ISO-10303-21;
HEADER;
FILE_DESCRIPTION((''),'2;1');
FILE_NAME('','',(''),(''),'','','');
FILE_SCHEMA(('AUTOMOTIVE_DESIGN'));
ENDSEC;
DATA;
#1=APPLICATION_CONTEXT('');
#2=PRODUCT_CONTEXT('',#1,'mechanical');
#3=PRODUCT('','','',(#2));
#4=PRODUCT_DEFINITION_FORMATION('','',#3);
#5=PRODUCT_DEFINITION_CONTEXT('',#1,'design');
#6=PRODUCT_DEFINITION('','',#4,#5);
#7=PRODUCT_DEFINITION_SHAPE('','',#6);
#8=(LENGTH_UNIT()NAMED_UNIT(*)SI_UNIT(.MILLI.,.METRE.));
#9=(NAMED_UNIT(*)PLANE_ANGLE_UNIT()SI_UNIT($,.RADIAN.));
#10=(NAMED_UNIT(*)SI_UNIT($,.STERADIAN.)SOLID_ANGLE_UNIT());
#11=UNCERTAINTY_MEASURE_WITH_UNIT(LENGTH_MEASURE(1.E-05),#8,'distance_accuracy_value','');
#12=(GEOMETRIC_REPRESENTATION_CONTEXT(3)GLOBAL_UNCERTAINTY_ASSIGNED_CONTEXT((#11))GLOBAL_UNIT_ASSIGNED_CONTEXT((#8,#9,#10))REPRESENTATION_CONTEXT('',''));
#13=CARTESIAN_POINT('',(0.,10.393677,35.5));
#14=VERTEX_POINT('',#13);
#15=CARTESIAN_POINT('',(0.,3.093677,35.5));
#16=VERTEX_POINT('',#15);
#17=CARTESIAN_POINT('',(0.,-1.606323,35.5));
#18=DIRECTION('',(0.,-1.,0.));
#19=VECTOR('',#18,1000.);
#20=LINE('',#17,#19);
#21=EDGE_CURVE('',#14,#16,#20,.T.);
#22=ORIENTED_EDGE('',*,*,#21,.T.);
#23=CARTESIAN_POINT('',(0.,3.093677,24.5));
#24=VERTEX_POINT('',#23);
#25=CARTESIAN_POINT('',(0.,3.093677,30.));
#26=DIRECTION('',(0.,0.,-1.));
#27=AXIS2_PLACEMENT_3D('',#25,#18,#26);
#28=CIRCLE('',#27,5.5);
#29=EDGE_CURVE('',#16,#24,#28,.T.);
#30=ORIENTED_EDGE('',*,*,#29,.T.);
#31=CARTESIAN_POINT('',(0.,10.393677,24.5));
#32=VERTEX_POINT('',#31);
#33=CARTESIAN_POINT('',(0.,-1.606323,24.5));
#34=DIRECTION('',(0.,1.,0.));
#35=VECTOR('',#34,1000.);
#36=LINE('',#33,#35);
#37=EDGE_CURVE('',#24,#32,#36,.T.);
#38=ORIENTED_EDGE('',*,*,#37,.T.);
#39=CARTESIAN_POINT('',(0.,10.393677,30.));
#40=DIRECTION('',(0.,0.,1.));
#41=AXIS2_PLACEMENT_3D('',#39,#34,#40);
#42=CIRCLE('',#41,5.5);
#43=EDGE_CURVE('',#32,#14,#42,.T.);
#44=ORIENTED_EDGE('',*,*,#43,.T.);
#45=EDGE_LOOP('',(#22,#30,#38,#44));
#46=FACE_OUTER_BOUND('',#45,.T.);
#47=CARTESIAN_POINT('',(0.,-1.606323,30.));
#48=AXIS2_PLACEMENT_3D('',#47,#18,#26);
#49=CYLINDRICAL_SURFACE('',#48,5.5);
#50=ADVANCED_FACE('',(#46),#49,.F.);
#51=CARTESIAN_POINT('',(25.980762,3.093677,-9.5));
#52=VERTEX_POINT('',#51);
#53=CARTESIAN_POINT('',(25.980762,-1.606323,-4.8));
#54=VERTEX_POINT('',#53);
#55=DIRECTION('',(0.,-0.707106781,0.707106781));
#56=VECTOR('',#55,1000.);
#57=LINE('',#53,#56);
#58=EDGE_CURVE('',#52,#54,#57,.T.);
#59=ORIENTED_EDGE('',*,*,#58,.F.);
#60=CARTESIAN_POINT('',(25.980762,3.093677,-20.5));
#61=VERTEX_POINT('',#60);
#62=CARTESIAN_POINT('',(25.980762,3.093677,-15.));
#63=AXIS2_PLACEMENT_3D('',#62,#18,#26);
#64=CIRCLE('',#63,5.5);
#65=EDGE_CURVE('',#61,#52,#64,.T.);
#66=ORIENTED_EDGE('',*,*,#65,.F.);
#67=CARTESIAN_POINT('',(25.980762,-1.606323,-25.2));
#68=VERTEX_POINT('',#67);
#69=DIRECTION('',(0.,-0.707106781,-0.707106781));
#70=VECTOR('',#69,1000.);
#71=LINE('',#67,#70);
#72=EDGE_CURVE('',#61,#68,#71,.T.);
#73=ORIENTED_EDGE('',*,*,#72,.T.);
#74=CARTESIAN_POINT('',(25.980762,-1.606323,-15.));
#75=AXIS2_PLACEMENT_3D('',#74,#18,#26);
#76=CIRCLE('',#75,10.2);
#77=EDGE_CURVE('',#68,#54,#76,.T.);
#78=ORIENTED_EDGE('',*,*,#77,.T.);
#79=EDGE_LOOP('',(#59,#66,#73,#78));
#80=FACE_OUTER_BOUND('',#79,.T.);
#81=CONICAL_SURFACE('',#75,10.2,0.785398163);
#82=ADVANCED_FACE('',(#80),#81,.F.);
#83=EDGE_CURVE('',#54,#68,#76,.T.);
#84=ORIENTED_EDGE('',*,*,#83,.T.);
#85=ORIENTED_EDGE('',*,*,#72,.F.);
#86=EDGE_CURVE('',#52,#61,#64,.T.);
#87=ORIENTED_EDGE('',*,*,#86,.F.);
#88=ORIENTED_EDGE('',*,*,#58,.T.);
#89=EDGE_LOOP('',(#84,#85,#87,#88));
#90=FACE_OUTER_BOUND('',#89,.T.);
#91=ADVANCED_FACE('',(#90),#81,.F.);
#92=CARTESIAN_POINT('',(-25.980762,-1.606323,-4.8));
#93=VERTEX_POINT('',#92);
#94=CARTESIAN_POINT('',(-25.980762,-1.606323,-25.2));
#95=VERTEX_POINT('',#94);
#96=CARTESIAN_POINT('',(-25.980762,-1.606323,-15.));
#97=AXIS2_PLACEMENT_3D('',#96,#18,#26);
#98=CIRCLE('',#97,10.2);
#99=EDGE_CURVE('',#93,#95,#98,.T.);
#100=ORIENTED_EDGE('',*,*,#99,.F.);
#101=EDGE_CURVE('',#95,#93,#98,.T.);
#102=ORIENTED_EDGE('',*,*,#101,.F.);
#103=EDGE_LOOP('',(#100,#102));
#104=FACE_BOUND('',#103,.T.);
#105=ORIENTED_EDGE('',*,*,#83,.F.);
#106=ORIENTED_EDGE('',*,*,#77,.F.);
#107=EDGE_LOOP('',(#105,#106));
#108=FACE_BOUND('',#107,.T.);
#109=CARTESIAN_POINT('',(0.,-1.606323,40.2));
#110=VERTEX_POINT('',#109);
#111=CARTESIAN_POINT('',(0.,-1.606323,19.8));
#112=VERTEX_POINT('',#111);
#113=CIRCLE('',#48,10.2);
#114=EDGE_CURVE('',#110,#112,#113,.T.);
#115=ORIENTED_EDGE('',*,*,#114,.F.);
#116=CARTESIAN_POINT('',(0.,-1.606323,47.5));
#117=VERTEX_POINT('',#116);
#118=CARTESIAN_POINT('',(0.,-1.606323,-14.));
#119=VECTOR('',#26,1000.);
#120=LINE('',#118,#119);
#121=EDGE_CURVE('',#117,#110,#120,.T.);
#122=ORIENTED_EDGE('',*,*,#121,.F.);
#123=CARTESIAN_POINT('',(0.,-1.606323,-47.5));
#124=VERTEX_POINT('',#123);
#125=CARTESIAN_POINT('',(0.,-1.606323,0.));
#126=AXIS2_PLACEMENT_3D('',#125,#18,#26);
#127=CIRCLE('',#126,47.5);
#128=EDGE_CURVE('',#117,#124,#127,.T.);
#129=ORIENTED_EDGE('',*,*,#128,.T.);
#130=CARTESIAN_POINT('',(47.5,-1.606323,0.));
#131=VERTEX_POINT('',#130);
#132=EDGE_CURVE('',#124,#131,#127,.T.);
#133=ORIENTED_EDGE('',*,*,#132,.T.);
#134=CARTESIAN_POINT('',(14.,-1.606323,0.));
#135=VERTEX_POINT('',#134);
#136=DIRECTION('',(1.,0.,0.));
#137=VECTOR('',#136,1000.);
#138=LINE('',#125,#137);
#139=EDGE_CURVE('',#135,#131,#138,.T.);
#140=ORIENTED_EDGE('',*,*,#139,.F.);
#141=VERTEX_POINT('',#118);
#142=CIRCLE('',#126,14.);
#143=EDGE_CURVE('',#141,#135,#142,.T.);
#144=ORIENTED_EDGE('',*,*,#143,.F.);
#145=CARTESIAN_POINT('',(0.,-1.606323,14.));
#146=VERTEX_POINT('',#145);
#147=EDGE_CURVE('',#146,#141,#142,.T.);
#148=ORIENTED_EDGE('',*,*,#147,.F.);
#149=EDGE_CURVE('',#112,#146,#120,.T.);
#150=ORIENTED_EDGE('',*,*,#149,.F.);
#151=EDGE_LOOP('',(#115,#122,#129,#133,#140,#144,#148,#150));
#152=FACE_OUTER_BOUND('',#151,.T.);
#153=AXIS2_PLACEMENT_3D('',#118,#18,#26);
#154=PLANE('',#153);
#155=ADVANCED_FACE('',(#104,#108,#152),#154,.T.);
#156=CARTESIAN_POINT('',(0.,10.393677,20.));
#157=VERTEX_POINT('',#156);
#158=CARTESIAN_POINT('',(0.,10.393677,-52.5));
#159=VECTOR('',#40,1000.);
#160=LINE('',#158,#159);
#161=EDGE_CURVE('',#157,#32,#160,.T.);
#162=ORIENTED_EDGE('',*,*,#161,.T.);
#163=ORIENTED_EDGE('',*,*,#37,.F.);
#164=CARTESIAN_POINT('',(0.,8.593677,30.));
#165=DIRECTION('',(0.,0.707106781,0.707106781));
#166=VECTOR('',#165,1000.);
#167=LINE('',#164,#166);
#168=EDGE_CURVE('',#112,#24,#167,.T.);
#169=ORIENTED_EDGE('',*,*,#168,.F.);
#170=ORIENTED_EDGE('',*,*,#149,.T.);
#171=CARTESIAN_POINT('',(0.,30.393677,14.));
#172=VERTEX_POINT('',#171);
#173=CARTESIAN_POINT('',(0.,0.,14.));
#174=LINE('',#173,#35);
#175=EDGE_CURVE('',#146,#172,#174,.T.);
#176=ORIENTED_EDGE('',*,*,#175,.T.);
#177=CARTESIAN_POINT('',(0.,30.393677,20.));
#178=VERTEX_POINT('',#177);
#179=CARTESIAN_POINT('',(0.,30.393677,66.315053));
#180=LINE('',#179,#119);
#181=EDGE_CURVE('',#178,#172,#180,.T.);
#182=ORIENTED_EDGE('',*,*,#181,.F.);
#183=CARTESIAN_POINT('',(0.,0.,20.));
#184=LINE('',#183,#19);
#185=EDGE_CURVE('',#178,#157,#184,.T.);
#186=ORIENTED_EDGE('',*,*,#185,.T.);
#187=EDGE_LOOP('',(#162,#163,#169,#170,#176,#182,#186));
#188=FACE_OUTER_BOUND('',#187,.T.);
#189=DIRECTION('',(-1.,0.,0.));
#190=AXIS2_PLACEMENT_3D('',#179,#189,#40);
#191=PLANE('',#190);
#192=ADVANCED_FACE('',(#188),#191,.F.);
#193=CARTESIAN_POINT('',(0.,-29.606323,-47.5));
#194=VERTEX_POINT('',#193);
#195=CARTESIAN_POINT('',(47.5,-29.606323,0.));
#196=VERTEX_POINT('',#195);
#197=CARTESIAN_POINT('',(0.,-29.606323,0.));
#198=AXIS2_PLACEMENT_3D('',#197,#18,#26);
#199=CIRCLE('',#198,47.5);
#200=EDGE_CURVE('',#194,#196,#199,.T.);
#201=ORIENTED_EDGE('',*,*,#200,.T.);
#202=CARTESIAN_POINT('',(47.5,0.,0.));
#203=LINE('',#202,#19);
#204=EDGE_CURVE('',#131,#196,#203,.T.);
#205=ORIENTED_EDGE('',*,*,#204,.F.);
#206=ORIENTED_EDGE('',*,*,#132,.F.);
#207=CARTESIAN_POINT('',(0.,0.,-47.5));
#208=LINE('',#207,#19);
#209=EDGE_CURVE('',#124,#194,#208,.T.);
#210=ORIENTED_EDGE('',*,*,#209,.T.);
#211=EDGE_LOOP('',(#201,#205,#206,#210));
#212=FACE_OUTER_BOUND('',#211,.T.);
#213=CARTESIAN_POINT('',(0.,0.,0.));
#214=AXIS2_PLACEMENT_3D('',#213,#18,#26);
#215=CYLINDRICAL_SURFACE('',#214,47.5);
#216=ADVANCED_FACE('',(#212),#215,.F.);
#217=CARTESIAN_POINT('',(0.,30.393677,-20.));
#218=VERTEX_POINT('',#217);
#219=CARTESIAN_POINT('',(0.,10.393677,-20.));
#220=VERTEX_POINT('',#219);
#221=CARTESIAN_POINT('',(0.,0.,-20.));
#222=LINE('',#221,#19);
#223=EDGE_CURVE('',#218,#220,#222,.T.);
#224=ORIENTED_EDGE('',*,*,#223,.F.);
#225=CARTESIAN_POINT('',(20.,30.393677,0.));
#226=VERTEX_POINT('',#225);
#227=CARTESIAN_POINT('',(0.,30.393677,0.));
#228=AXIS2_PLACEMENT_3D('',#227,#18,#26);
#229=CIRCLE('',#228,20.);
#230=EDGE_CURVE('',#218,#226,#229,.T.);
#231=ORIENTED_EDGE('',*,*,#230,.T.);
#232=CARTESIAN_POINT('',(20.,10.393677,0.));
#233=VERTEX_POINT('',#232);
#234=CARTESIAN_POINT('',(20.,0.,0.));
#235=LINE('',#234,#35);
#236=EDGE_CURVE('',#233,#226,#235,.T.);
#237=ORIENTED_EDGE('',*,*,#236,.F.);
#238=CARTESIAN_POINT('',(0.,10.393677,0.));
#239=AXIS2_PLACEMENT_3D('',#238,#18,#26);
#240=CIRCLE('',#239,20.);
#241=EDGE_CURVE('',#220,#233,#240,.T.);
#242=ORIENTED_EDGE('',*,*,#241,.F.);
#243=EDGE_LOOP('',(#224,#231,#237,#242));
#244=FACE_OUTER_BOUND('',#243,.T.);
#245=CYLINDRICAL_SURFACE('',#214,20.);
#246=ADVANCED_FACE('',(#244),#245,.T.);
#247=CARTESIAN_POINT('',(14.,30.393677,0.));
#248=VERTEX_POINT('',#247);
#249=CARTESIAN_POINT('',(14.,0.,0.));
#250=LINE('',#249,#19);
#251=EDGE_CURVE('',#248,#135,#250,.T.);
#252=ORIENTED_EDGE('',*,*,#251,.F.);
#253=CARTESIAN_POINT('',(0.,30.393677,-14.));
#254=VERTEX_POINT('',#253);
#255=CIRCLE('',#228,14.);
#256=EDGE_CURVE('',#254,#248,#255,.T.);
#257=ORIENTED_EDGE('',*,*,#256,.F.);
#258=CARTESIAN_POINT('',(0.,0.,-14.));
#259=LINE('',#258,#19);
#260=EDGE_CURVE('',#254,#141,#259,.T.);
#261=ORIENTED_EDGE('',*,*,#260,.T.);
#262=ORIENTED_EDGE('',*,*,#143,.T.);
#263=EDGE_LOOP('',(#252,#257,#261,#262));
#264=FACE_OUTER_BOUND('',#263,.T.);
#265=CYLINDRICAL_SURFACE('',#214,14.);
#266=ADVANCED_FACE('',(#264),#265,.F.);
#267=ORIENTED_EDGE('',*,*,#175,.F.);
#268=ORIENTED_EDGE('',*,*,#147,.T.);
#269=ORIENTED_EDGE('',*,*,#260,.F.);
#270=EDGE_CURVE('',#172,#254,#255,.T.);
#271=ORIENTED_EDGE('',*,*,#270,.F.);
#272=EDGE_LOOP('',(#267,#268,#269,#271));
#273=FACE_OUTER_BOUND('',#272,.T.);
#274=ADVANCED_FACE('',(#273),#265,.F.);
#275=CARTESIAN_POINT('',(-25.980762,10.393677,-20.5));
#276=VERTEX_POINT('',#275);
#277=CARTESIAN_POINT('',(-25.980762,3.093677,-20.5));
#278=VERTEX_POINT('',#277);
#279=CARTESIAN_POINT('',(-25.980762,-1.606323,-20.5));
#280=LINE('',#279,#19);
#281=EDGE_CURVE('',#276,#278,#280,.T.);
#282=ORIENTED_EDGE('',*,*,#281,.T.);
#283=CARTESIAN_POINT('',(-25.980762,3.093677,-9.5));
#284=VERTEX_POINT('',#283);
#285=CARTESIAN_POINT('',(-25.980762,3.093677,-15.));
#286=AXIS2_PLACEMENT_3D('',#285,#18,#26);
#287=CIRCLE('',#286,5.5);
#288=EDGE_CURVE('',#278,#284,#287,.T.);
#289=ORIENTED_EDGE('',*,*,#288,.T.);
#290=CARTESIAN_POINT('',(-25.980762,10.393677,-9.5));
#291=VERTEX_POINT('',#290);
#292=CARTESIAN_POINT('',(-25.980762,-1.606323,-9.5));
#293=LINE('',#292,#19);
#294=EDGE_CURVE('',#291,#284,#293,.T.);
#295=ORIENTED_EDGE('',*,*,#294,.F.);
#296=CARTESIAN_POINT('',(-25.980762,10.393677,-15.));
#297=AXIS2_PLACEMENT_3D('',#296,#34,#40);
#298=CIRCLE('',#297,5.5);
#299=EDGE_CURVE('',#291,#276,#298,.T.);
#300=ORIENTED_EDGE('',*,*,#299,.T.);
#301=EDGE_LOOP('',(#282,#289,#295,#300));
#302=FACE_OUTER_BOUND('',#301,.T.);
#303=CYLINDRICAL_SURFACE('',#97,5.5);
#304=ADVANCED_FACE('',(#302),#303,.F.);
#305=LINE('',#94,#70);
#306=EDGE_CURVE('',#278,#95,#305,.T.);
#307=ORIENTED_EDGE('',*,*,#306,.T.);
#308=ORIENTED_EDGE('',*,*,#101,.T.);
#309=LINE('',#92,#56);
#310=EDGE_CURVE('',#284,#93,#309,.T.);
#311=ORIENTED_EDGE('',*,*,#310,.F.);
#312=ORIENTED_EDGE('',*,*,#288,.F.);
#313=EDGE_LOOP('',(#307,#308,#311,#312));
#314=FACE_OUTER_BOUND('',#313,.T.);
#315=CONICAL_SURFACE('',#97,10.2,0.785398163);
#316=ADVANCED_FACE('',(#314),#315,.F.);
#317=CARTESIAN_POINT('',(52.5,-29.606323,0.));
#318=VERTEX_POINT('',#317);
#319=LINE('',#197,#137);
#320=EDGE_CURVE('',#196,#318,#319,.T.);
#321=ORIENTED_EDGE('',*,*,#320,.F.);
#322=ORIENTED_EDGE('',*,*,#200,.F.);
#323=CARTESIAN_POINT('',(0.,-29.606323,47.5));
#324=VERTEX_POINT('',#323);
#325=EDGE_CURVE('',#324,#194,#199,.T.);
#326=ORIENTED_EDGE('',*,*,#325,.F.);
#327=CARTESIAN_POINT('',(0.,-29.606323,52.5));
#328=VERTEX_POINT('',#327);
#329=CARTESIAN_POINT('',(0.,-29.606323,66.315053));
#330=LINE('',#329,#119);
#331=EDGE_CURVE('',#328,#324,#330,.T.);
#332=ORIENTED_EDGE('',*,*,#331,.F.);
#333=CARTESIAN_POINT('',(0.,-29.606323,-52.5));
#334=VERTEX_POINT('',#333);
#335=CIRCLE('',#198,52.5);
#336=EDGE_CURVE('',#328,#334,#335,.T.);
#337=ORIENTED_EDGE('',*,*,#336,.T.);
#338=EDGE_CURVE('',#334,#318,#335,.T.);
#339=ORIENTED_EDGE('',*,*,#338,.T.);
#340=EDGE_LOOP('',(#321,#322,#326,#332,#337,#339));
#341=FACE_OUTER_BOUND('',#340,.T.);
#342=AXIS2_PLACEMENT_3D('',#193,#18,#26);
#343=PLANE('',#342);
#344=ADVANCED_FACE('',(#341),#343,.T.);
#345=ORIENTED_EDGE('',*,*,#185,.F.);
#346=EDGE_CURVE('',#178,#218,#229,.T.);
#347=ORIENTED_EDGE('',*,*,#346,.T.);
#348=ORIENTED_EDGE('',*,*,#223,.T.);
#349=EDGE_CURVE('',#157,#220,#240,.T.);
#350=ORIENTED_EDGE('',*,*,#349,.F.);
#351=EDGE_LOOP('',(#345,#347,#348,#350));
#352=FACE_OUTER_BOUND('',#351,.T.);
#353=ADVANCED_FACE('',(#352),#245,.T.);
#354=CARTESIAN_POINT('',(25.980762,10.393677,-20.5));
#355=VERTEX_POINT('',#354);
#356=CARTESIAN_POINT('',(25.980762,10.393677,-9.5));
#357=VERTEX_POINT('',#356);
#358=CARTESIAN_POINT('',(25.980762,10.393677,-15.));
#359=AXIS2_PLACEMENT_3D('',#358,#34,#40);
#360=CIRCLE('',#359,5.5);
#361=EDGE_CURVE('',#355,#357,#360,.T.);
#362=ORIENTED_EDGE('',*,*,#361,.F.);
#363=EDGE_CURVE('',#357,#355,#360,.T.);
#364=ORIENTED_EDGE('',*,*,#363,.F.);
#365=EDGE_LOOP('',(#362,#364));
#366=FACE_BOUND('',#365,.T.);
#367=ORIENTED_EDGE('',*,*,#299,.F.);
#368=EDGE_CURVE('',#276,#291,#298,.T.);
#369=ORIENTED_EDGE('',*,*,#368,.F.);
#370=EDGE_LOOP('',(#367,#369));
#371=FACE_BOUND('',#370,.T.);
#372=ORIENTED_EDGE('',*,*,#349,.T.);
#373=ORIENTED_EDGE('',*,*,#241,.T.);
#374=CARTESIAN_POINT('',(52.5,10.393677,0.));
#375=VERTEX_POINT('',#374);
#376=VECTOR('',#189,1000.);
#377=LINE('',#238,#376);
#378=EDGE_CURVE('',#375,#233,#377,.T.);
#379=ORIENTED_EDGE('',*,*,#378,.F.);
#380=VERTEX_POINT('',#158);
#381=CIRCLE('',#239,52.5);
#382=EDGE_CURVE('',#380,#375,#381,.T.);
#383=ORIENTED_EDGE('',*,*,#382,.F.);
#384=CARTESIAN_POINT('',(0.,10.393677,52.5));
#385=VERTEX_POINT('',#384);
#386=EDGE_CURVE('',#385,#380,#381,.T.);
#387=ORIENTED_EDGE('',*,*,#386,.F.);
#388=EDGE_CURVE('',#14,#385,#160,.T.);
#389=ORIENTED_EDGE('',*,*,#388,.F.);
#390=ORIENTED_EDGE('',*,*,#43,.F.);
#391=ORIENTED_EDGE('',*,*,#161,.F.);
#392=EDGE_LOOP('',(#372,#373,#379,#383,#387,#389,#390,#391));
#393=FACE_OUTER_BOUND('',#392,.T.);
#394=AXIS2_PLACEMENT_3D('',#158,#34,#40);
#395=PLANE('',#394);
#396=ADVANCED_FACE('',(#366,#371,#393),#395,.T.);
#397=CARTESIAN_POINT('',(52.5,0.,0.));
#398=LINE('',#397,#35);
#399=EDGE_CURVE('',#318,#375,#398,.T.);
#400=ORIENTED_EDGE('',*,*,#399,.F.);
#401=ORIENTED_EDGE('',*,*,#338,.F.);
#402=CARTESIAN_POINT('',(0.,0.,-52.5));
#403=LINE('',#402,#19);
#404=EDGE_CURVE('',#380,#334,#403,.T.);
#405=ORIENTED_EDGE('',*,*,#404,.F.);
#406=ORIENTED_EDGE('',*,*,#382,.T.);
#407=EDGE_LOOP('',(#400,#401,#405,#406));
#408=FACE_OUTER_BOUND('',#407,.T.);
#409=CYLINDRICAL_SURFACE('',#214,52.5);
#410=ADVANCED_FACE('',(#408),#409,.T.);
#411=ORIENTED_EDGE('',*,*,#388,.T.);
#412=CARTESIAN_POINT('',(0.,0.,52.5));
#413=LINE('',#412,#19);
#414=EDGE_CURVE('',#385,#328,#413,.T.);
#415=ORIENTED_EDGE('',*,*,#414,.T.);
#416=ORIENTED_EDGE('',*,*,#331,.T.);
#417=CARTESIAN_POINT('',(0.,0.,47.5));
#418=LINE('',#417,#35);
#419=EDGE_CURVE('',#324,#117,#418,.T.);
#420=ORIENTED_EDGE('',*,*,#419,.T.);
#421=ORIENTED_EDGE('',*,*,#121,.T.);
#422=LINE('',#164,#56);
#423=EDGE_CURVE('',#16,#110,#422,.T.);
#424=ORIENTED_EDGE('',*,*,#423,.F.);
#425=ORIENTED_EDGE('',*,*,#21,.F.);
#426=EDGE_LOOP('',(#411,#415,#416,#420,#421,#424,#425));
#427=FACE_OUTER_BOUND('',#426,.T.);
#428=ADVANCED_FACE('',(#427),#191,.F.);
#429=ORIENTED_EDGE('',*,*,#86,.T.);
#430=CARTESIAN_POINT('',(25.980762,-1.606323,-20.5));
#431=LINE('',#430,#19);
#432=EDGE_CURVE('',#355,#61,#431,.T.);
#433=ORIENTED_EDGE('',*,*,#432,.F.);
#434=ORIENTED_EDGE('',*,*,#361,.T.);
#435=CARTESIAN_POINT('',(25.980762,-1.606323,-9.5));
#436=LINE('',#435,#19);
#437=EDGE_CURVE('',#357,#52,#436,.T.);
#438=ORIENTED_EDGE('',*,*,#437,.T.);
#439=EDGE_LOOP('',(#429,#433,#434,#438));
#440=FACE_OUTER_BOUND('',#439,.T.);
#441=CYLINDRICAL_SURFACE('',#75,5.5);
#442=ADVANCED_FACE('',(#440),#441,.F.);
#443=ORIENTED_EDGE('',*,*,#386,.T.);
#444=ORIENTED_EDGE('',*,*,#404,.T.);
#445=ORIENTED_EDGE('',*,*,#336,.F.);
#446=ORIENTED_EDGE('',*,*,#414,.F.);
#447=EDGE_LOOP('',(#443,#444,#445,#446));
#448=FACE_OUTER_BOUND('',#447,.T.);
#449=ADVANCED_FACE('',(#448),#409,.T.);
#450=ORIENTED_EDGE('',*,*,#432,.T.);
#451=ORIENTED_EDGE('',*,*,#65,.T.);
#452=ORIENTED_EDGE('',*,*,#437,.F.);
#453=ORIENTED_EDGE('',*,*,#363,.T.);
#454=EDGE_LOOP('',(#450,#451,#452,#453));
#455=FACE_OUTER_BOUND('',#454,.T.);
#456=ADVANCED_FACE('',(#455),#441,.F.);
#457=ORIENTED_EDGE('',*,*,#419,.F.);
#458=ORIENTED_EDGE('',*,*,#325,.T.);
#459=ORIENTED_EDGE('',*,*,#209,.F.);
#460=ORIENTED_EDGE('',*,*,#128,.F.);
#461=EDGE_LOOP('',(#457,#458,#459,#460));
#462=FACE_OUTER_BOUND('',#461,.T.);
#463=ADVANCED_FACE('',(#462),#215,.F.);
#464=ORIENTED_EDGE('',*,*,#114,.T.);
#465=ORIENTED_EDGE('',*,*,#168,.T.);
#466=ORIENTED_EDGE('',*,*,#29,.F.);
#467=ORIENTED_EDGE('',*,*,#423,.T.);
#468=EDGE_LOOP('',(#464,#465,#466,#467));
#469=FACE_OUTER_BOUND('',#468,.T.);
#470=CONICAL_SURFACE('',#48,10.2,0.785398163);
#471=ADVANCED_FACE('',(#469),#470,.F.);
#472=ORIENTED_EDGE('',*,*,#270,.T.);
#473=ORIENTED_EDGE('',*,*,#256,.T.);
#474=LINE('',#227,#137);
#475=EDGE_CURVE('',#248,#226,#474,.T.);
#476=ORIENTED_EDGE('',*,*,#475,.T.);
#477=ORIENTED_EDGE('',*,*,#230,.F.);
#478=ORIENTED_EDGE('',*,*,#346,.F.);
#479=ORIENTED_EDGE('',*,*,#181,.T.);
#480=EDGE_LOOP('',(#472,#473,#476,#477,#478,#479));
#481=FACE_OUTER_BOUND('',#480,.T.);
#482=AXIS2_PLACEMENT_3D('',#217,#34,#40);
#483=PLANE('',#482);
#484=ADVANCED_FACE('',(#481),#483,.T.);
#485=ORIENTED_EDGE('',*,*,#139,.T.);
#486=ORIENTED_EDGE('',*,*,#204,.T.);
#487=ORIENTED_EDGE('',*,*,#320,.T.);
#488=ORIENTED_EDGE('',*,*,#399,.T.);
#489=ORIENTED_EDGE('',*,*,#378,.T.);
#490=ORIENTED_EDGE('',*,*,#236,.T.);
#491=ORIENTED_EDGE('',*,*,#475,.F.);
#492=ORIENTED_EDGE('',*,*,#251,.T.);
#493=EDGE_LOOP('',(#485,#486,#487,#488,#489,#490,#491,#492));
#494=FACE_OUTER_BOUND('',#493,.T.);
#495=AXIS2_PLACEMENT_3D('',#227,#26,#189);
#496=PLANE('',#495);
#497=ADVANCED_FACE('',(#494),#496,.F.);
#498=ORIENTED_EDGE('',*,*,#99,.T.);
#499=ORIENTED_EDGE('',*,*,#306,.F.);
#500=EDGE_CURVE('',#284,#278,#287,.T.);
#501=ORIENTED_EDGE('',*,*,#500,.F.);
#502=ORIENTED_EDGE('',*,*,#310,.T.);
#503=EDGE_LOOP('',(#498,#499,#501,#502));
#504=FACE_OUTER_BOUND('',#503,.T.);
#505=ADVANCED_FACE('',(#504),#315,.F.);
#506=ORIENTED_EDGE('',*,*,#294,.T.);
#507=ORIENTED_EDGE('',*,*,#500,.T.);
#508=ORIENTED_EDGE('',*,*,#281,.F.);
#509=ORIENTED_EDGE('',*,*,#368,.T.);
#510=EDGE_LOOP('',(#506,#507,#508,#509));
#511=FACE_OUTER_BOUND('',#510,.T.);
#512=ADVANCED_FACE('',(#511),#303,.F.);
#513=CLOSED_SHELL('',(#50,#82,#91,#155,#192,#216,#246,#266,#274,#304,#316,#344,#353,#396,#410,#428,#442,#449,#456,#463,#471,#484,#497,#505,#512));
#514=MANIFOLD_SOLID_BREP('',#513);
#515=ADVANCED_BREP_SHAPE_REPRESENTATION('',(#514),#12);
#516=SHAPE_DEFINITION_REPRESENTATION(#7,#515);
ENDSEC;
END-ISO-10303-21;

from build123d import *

# Parameters (mm, degrees)
COUNTERSUNK_HOLE_11_D             = 11
COUNTERSUNK_HOLE_11_CSINK_D       = 20.4
COUNTERSUNK_HOLE_11_CSINK_ANGLE   = 90
COUNTERSUNK_HOLE_PATTERN_3X_COUNT = 3
SIDE_SLOT_CUT_DEPTH               = 81.848623983
SIDE_SLOT_CUT_DEPTH_BACK          = 81.848623983


with BuildPart() as part:
    # Bed Profile Sketch → Bed Body Revolve (revolve)
    with BuildSketch(Plane(origin=(0, 0, 0), x_dir=(0, 0, -1), z_dir=(1, 0, 0))):
        Polygon((14, 30.393677345), (14, -1.606322655), (47.5, -1.606322655), (47.5, -29.606322655), (52.5, -29.606322655), (52.5, 10.393677345), (20, 10.393677345), (20, 30.393677345), align=None)
    revolve(axis=Axis((0, 0, 0), (0, 1, 0)))

    # Countersunk Hole Ø11 (through all)
    with Locations(Plane(origin=(0, -1.606322655, 30), x_dir=(0, 0, -1), z_dir=(0, -1, 0))):
        with Locations((0, 0)):
            countersunk_hole_11 = CounterSinkHole(COUNTERSUNK_HOLE_11_D / 2, COUNTERSUNK_HOLE_11_CSINK_D / 2, counter_sink_angle=COUNTERSUNK_HOLE_11_CSINK_ANGLE)

    # Countersunk Hole Pattern 3x: Countersunk Hole Ø11 ×3 about axis
    countersunk_hole_pattern_3x_axis = Axis((0, 0, 0), (0, 1, 0))
    for i in range(1, COUNTERSUNK_HOLE_PATTERN_3X_COUNT):
        add(countersunk_hole_11.rotate(countersunk_hole_pattern_3x_axis, i * 360 / COUNTERSUNK_HOLE_PATTERN_3X_COUNT), mode=Mode.SUBTRACT)

    # Side Slot Sketch → Side Slot Cut (cut, two sides: drawn at the far end of the back side and taken through both)
    with BuildSketch(Plane.XZ.offset(1.606322655).offset(-SIDE_SLOT_CUT_DEPTH_BACK)):
        with BuildLine():
            Line((0, 66.315052509), (0, 0))
            Line((0, 0), (70.372177226, 0))
            ThreePointArc((70.372177226, 0), (52.403266899, 51.428043669), (0, 66.315052509))
        make_face()
    extrude(amount=SIDE_SLOT_CUT_DEPTH + SIDE_SLOT_CUT_DEPTH_BACK, mode=Mode.SUBTRACT)


solid = part.part
